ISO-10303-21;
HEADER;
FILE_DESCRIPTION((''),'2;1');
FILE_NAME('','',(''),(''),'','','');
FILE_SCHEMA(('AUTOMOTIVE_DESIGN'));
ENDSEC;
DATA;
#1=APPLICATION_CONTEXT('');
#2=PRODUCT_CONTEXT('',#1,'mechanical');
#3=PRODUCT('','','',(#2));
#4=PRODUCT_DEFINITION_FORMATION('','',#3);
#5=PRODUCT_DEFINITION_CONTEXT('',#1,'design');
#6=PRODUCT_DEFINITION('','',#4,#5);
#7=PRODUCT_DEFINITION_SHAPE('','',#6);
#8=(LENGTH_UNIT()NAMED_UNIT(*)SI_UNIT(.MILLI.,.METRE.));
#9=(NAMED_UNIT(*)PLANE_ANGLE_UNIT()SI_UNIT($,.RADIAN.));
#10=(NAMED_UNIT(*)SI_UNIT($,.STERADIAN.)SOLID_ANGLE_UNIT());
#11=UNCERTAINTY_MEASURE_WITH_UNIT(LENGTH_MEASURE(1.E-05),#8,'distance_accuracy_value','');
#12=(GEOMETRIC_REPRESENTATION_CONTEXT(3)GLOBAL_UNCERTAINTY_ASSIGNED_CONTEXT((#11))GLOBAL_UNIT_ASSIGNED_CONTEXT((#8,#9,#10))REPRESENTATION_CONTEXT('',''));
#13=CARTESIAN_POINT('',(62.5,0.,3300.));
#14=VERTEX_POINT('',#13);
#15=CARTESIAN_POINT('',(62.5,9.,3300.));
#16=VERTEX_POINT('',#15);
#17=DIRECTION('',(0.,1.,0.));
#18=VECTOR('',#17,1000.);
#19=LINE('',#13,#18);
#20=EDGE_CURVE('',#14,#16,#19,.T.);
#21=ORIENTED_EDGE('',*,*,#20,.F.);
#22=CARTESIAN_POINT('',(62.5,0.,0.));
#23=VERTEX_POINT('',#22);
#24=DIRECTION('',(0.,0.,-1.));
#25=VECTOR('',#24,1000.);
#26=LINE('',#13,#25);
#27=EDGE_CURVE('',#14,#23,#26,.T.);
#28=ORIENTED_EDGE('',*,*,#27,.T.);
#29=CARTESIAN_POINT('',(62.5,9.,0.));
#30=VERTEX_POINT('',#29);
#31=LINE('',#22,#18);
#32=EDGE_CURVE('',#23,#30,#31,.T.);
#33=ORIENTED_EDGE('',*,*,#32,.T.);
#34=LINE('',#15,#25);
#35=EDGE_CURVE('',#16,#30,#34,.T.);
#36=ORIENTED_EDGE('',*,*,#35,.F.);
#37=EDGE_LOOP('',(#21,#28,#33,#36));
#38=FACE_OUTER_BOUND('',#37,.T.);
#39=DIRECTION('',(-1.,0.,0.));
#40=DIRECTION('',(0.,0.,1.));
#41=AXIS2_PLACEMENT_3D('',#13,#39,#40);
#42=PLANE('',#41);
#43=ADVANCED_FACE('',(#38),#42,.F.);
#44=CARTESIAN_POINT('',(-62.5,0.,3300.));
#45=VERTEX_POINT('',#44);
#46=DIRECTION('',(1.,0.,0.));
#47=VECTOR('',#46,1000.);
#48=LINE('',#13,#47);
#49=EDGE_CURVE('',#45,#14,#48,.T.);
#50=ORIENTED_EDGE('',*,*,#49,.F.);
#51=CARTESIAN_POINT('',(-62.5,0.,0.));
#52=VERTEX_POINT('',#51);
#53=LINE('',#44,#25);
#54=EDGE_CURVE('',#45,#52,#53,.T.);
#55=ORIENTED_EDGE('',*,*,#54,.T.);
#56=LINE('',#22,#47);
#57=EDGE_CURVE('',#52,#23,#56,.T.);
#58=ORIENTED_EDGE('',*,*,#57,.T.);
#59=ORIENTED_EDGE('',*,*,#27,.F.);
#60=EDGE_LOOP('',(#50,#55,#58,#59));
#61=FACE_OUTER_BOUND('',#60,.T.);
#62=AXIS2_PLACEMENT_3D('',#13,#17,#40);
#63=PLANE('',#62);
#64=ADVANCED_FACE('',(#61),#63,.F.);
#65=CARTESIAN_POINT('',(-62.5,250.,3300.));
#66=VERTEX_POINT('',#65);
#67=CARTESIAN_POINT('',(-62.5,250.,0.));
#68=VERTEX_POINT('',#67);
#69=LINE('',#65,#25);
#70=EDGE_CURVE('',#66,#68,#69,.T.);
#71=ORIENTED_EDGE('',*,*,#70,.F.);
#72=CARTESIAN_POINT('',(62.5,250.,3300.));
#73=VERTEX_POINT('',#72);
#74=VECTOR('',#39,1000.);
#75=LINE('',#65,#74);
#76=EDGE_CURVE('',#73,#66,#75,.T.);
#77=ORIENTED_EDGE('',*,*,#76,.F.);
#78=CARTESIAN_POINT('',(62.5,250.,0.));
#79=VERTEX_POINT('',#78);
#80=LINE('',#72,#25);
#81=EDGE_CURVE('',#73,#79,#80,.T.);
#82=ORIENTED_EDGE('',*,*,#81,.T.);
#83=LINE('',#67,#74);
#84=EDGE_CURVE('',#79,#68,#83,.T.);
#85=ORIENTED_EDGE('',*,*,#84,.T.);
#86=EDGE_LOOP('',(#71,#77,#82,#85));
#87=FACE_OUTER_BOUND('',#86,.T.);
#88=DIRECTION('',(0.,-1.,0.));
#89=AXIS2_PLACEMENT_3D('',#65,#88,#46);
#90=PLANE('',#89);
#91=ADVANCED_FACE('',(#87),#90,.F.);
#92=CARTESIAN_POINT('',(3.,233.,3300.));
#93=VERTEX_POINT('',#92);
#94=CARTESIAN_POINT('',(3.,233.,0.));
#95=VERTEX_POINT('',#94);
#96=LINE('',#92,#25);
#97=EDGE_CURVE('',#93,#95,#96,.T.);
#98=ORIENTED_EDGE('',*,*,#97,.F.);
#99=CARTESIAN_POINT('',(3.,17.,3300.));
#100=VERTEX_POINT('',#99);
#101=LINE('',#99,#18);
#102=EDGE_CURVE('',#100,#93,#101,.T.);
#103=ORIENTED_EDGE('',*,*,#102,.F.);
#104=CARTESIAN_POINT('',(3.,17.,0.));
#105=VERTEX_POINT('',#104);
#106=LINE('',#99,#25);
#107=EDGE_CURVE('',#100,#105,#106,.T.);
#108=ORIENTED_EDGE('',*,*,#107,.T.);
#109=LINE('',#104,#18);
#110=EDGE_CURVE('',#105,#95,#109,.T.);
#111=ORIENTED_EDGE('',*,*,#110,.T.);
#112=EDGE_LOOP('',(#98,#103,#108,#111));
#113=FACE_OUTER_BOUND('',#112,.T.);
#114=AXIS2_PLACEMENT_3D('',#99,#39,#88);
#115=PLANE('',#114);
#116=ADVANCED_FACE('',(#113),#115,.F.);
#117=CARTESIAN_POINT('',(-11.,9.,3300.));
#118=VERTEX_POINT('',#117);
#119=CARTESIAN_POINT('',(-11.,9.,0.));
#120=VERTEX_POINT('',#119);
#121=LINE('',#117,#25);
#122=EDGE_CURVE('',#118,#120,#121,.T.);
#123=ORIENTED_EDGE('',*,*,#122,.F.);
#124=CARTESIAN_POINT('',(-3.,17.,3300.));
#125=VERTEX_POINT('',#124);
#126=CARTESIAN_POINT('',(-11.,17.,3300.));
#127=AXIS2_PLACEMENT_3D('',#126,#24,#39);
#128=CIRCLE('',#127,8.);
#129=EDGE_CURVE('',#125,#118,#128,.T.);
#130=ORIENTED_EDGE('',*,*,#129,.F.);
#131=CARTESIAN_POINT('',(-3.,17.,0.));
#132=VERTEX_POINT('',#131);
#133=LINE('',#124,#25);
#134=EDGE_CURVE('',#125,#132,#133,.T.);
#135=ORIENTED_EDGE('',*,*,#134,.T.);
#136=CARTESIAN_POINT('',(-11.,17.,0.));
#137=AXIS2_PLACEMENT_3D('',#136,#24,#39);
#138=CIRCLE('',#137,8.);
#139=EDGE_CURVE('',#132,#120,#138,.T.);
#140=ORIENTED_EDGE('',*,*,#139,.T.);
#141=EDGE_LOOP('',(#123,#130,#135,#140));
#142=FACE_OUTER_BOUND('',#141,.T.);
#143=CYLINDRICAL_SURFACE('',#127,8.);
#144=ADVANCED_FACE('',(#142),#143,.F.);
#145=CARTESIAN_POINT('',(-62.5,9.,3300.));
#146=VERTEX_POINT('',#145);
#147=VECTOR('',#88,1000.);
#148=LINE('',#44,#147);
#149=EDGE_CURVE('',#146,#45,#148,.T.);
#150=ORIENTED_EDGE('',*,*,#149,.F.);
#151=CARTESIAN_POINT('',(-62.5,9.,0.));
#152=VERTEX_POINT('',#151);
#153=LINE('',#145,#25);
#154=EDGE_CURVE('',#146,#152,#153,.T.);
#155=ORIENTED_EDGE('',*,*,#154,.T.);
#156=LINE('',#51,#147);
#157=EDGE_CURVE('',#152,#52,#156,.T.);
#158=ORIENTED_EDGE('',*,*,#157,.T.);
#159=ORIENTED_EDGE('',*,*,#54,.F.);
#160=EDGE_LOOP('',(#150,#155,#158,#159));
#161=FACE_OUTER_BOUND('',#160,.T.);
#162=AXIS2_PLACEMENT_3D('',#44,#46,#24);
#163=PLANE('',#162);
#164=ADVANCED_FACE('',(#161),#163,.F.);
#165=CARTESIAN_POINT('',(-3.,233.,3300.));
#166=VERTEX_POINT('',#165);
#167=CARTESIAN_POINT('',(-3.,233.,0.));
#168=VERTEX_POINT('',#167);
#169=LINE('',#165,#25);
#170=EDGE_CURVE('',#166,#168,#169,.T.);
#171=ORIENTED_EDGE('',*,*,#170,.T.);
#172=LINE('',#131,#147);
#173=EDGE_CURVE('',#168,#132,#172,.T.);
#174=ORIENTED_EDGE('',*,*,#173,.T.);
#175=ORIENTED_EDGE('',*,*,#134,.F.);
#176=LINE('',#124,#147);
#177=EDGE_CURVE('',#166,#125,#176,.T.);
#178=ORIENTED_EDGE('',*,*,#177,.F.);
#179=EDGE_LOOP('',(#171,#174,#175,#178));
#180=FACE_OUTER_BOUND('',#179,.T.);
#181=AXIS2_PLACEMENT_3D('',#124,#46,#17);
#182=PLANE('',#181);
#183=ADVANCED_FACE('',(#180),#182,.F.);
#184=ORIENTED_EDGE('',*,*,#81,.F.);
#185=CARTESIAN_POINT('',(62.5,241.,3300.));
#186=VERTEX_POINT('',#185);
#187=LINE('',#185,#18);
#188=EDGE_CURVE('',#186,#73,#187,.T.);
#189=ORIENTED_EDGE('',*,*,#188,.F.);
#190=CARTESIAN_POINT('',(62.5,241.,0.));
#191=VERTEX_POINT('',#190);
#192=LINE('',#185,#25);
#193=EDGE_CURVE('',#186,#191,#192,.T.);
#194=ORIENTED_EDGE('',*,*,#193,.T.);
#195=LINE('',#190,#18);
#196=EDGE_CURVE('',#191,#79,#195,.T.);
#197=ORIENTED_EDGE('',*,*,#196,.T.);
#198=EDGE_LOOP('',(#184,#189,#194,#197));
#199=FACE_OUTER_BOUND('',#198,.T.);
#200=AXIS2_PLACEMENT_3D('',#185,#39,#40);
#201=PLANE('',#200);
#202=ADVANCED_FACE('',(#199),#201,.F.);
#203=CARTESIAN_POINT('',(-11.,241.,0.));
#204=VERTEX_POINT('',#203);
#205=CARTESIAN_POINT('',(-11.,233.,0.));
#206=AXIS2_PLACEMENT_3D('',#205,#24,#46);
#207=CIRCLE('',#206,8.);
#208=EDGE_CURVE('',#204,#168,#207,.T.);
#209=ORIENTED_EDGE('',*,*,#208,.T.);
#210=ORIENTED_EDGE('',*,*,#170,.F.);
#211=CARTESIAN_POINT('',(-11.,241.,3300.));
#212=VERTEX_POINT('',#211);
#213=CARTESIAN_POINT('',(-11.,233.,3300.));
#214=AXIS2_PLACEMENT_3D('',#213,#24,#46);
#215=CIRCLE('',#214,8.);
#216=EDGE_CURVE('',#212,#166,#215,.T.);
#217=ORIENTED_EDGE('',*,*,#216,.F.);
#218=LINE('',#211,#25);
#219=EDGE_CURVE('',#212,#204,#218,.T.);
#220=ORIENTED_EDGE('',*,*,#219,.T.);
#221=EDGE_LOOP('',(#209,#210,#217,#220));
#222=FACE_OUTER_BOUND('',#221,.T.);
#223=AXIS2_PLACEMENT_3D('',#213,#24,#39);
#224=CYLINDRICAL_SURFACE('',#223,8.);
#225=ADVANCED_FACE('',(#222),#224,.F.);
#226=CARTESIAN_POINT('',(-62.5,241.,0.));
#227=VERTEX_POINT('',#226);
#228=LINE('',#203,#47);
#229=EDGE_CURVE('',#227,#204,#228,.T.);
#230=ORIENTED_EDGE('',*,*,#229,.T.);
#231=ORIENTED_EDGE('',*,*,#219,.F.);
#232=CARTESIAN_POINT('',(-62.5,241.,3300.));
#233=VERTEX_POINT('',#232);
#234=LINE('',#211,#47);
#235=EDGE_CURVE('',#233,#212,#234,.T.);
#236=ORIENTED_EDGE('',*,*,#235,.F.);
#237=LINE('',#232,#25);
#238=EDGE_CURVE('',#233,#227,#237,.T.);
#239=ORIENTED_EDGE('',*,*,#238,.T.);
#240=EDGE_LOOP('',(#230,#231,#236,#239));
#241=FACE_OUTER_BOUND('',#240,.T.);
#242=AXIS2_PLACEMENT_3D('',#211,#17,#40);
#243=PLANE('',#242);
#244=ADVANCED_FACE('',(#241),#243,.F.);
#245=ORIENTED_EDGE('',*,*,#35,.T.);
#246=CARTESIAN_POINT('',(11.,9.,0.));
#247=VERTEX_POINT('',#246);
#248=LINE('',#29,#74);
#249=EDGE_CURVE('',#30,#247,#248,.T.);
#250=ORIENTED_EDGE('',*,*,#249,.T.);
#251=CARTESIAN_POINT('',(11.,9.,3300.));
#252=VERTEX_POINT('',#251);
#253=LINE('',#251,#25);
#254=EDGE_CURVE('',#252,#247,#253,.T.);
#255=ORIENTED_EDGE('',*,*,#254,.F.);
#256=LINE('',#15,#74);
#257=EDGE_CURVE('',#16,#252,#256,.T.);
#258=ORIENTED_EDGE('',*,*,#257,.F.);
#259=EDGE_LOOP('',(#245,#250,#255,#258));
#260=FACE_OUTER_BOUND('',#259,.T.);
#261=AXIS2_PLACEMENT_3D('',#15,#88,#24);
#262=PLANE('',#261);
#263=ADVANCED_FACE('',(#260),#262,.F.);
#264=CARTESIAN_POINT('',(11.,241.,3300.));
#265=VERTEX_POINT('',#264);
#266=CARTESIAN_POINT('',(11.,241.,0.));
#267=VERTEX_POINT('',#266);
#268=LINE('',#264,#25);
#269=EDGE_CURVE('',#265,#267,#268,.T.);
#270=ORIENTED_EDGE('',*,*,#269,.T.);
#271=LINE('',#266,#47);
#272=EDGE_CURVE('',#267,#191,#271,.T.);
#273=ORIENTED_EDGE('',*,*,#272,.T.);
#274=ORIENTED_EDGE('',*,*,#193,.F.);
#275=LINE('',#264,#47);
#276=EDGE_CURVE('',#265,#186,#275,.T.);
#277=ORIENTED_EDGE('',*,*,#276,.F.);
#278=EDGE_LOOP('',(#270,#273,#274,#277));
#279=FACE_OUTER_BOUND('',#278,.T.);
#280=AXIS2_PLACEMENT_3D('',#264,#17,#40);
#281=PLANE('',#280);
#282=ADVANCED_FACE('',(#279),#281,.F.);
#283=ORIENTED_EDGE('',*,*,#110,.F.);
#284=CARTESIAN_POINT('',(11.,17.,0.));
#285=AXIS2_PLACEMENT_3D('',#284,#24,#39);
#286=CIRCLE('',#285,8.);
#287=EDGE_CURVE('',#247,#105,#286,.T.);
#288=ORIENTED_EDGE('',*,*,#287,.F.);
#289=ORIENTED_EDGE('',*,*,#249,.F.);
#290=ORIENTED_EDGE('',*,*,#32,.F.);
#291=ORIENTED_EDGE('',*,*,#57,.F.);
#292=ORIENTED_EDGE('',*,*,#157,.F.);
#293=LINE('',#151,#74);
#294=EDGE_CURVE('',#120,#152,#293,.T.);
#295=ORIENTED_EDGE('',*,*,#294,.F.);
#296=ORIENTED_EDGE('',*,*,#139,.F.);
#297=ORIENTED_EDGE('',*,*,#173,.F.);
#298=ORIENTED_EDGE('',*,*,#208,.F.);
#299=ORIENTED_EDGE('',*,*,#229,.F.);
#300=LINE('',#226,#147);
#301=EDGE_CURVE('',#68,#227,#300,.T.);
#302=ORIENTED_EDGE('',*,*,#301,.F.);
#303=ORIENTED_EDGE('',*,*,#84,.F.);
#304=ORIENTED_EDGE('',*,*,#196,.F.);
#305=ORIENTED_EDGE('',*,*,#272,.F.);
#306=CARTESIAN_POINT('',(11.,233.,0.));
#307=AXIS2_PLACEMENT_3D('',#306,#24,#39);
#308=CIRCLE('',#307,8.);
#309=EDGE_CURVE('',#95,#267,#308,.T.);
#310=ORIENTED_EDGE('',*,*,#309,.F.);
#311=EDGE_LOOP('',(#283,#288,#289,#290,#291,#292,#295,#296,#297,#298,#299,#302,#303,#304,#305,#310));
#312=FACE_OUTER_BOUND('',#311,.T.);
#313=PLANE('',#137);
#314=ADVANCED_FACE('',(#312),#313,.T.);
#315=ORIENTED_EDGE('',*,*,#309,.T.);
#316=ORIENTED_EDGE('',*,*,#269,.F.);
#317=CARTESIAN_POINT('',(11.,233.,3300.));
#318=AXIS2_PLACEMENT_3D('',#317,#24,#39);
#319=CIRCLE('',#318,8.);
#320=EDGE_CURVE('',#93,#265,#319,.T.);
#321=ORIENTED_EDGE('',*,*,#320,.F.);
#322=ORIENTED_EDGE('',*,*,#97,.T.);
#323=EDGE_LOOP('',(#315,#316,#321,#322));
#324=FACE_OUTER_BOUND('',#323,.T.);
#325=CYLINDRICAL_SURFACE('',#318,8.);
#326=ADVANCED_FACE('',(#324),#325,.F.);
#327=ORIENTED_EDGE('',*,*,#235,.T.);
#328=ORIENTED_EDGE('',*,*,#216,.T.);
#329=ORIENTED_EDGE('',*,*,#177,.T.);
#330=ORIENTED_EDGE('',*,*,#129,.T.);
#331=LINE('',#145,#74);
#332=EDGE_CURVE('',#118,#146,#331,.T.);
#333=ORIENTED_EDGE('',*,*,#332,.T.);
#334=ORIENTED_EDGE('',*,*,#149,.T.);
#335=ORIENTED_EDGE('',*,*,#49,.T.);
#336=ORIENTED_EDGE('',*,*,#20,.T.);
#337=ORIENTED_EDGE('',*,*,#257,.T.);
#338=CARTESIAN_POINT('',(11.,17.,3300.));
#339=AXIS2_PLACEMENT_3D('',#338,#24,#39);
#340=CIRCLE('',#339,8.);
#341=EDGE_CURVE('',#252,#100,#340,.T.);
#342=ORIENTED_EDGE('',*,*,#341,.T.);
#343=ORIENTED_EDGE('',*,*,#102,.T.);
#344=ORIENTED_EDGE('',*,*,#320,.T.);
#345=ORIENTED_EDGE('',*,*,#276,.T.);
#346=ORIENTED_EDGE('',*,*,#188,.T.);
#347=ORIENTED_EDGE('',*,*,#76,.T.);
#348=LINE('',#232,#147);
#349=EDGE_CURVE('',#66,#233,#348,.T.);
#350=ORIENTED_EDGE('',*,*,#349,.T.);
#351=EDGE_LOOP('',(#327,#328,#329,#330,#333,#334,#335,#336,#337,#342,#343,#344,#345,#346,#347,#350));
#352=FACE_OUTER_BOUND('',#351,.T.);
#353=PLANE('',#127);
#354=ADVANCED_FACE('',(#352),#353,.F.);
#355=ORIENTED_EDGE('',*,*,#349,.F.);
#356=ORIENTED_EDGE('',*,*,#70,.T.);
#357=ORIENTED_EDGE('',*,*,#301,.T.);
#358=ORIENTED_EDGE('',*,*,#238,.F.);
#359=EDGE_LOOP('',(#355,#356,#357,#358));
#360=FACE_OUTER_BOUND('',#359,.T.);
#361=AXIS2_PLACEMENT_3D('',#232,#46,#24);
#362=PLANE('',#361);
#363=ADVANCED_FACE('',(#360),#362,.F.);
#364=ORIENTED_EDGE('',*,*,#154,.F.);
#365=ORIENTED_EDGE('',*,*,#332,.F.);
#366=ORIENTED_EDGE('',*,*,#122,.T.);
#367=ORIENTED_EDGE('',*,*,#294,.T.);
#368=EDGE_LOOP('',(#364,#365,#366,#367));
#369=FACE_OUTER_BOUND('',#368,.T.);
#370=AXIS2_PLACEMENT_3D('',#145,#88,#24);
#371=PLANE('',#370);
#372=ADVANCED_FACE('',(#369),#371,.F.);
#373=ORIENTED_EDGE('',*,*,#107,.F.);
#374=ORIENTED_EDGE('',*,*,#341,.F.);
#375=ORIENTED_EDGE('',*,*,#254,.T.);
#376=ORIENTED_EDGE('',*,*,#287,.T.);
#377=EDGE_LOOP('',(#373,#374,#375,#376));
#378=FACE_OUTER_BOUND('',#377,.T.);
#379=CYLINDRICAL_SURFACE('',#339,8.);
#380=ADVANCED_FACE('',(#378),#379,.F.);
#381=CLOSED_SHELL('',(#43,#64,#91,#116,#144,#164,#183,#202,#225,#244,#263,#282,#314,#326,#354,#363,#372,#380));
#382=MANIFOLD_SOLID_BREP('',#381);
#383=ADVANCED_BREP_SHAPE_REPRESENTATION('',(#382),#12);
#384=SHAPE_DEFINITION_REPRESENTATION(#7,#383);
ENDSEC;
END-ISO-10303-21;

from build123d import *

# Parameters (mm, degrees)
BOSS_EXTRUDE1_DEPTH = 3300


with BuildPart() as part:
    # Sketch1 → Boss-Extrude1 (new body)
    with BuildSketch(Plane.XY):
        with BuildLine():
            Line((62.5, 0), (-62.5, 0))
            Line((-62.5, 0), (-62.5, 9))
            Line((-62.5, 9), (-11, 9))
            ThreePointArc((-11, 9), (-5.343145751, 11.343145751), (-3, 17))
            Line((-3, 17), (-3, 233))
            ThreePointArc((-3, 233), (-5.343145751, 238.656854249), (-11, 241))
            Line((-11, 241), (-62.5, 241))
            Line((-62.5, 241), (-62.5, 250))
            Line((-62.5, 250), (62.5, 250))
            Line((62.5, 250), (62.5, 241))
            Line((62.5, 241), (11, 241))
            ThreePointArc((11, 241), (5.343145751, 238.656854249), (3, 233))
            Line((3, 233), (3, 17))
            ThreePointArc((3, 17), (5.343145751, 11.343145751), (11, 9))
            Line((11, 9), (62.5, 9))
            Line((62.5, 9), (62.5, 0))
        make_face()
    extrude(amount=BOSS_EXTRUDE1_DEPTH)


solid = part.part
